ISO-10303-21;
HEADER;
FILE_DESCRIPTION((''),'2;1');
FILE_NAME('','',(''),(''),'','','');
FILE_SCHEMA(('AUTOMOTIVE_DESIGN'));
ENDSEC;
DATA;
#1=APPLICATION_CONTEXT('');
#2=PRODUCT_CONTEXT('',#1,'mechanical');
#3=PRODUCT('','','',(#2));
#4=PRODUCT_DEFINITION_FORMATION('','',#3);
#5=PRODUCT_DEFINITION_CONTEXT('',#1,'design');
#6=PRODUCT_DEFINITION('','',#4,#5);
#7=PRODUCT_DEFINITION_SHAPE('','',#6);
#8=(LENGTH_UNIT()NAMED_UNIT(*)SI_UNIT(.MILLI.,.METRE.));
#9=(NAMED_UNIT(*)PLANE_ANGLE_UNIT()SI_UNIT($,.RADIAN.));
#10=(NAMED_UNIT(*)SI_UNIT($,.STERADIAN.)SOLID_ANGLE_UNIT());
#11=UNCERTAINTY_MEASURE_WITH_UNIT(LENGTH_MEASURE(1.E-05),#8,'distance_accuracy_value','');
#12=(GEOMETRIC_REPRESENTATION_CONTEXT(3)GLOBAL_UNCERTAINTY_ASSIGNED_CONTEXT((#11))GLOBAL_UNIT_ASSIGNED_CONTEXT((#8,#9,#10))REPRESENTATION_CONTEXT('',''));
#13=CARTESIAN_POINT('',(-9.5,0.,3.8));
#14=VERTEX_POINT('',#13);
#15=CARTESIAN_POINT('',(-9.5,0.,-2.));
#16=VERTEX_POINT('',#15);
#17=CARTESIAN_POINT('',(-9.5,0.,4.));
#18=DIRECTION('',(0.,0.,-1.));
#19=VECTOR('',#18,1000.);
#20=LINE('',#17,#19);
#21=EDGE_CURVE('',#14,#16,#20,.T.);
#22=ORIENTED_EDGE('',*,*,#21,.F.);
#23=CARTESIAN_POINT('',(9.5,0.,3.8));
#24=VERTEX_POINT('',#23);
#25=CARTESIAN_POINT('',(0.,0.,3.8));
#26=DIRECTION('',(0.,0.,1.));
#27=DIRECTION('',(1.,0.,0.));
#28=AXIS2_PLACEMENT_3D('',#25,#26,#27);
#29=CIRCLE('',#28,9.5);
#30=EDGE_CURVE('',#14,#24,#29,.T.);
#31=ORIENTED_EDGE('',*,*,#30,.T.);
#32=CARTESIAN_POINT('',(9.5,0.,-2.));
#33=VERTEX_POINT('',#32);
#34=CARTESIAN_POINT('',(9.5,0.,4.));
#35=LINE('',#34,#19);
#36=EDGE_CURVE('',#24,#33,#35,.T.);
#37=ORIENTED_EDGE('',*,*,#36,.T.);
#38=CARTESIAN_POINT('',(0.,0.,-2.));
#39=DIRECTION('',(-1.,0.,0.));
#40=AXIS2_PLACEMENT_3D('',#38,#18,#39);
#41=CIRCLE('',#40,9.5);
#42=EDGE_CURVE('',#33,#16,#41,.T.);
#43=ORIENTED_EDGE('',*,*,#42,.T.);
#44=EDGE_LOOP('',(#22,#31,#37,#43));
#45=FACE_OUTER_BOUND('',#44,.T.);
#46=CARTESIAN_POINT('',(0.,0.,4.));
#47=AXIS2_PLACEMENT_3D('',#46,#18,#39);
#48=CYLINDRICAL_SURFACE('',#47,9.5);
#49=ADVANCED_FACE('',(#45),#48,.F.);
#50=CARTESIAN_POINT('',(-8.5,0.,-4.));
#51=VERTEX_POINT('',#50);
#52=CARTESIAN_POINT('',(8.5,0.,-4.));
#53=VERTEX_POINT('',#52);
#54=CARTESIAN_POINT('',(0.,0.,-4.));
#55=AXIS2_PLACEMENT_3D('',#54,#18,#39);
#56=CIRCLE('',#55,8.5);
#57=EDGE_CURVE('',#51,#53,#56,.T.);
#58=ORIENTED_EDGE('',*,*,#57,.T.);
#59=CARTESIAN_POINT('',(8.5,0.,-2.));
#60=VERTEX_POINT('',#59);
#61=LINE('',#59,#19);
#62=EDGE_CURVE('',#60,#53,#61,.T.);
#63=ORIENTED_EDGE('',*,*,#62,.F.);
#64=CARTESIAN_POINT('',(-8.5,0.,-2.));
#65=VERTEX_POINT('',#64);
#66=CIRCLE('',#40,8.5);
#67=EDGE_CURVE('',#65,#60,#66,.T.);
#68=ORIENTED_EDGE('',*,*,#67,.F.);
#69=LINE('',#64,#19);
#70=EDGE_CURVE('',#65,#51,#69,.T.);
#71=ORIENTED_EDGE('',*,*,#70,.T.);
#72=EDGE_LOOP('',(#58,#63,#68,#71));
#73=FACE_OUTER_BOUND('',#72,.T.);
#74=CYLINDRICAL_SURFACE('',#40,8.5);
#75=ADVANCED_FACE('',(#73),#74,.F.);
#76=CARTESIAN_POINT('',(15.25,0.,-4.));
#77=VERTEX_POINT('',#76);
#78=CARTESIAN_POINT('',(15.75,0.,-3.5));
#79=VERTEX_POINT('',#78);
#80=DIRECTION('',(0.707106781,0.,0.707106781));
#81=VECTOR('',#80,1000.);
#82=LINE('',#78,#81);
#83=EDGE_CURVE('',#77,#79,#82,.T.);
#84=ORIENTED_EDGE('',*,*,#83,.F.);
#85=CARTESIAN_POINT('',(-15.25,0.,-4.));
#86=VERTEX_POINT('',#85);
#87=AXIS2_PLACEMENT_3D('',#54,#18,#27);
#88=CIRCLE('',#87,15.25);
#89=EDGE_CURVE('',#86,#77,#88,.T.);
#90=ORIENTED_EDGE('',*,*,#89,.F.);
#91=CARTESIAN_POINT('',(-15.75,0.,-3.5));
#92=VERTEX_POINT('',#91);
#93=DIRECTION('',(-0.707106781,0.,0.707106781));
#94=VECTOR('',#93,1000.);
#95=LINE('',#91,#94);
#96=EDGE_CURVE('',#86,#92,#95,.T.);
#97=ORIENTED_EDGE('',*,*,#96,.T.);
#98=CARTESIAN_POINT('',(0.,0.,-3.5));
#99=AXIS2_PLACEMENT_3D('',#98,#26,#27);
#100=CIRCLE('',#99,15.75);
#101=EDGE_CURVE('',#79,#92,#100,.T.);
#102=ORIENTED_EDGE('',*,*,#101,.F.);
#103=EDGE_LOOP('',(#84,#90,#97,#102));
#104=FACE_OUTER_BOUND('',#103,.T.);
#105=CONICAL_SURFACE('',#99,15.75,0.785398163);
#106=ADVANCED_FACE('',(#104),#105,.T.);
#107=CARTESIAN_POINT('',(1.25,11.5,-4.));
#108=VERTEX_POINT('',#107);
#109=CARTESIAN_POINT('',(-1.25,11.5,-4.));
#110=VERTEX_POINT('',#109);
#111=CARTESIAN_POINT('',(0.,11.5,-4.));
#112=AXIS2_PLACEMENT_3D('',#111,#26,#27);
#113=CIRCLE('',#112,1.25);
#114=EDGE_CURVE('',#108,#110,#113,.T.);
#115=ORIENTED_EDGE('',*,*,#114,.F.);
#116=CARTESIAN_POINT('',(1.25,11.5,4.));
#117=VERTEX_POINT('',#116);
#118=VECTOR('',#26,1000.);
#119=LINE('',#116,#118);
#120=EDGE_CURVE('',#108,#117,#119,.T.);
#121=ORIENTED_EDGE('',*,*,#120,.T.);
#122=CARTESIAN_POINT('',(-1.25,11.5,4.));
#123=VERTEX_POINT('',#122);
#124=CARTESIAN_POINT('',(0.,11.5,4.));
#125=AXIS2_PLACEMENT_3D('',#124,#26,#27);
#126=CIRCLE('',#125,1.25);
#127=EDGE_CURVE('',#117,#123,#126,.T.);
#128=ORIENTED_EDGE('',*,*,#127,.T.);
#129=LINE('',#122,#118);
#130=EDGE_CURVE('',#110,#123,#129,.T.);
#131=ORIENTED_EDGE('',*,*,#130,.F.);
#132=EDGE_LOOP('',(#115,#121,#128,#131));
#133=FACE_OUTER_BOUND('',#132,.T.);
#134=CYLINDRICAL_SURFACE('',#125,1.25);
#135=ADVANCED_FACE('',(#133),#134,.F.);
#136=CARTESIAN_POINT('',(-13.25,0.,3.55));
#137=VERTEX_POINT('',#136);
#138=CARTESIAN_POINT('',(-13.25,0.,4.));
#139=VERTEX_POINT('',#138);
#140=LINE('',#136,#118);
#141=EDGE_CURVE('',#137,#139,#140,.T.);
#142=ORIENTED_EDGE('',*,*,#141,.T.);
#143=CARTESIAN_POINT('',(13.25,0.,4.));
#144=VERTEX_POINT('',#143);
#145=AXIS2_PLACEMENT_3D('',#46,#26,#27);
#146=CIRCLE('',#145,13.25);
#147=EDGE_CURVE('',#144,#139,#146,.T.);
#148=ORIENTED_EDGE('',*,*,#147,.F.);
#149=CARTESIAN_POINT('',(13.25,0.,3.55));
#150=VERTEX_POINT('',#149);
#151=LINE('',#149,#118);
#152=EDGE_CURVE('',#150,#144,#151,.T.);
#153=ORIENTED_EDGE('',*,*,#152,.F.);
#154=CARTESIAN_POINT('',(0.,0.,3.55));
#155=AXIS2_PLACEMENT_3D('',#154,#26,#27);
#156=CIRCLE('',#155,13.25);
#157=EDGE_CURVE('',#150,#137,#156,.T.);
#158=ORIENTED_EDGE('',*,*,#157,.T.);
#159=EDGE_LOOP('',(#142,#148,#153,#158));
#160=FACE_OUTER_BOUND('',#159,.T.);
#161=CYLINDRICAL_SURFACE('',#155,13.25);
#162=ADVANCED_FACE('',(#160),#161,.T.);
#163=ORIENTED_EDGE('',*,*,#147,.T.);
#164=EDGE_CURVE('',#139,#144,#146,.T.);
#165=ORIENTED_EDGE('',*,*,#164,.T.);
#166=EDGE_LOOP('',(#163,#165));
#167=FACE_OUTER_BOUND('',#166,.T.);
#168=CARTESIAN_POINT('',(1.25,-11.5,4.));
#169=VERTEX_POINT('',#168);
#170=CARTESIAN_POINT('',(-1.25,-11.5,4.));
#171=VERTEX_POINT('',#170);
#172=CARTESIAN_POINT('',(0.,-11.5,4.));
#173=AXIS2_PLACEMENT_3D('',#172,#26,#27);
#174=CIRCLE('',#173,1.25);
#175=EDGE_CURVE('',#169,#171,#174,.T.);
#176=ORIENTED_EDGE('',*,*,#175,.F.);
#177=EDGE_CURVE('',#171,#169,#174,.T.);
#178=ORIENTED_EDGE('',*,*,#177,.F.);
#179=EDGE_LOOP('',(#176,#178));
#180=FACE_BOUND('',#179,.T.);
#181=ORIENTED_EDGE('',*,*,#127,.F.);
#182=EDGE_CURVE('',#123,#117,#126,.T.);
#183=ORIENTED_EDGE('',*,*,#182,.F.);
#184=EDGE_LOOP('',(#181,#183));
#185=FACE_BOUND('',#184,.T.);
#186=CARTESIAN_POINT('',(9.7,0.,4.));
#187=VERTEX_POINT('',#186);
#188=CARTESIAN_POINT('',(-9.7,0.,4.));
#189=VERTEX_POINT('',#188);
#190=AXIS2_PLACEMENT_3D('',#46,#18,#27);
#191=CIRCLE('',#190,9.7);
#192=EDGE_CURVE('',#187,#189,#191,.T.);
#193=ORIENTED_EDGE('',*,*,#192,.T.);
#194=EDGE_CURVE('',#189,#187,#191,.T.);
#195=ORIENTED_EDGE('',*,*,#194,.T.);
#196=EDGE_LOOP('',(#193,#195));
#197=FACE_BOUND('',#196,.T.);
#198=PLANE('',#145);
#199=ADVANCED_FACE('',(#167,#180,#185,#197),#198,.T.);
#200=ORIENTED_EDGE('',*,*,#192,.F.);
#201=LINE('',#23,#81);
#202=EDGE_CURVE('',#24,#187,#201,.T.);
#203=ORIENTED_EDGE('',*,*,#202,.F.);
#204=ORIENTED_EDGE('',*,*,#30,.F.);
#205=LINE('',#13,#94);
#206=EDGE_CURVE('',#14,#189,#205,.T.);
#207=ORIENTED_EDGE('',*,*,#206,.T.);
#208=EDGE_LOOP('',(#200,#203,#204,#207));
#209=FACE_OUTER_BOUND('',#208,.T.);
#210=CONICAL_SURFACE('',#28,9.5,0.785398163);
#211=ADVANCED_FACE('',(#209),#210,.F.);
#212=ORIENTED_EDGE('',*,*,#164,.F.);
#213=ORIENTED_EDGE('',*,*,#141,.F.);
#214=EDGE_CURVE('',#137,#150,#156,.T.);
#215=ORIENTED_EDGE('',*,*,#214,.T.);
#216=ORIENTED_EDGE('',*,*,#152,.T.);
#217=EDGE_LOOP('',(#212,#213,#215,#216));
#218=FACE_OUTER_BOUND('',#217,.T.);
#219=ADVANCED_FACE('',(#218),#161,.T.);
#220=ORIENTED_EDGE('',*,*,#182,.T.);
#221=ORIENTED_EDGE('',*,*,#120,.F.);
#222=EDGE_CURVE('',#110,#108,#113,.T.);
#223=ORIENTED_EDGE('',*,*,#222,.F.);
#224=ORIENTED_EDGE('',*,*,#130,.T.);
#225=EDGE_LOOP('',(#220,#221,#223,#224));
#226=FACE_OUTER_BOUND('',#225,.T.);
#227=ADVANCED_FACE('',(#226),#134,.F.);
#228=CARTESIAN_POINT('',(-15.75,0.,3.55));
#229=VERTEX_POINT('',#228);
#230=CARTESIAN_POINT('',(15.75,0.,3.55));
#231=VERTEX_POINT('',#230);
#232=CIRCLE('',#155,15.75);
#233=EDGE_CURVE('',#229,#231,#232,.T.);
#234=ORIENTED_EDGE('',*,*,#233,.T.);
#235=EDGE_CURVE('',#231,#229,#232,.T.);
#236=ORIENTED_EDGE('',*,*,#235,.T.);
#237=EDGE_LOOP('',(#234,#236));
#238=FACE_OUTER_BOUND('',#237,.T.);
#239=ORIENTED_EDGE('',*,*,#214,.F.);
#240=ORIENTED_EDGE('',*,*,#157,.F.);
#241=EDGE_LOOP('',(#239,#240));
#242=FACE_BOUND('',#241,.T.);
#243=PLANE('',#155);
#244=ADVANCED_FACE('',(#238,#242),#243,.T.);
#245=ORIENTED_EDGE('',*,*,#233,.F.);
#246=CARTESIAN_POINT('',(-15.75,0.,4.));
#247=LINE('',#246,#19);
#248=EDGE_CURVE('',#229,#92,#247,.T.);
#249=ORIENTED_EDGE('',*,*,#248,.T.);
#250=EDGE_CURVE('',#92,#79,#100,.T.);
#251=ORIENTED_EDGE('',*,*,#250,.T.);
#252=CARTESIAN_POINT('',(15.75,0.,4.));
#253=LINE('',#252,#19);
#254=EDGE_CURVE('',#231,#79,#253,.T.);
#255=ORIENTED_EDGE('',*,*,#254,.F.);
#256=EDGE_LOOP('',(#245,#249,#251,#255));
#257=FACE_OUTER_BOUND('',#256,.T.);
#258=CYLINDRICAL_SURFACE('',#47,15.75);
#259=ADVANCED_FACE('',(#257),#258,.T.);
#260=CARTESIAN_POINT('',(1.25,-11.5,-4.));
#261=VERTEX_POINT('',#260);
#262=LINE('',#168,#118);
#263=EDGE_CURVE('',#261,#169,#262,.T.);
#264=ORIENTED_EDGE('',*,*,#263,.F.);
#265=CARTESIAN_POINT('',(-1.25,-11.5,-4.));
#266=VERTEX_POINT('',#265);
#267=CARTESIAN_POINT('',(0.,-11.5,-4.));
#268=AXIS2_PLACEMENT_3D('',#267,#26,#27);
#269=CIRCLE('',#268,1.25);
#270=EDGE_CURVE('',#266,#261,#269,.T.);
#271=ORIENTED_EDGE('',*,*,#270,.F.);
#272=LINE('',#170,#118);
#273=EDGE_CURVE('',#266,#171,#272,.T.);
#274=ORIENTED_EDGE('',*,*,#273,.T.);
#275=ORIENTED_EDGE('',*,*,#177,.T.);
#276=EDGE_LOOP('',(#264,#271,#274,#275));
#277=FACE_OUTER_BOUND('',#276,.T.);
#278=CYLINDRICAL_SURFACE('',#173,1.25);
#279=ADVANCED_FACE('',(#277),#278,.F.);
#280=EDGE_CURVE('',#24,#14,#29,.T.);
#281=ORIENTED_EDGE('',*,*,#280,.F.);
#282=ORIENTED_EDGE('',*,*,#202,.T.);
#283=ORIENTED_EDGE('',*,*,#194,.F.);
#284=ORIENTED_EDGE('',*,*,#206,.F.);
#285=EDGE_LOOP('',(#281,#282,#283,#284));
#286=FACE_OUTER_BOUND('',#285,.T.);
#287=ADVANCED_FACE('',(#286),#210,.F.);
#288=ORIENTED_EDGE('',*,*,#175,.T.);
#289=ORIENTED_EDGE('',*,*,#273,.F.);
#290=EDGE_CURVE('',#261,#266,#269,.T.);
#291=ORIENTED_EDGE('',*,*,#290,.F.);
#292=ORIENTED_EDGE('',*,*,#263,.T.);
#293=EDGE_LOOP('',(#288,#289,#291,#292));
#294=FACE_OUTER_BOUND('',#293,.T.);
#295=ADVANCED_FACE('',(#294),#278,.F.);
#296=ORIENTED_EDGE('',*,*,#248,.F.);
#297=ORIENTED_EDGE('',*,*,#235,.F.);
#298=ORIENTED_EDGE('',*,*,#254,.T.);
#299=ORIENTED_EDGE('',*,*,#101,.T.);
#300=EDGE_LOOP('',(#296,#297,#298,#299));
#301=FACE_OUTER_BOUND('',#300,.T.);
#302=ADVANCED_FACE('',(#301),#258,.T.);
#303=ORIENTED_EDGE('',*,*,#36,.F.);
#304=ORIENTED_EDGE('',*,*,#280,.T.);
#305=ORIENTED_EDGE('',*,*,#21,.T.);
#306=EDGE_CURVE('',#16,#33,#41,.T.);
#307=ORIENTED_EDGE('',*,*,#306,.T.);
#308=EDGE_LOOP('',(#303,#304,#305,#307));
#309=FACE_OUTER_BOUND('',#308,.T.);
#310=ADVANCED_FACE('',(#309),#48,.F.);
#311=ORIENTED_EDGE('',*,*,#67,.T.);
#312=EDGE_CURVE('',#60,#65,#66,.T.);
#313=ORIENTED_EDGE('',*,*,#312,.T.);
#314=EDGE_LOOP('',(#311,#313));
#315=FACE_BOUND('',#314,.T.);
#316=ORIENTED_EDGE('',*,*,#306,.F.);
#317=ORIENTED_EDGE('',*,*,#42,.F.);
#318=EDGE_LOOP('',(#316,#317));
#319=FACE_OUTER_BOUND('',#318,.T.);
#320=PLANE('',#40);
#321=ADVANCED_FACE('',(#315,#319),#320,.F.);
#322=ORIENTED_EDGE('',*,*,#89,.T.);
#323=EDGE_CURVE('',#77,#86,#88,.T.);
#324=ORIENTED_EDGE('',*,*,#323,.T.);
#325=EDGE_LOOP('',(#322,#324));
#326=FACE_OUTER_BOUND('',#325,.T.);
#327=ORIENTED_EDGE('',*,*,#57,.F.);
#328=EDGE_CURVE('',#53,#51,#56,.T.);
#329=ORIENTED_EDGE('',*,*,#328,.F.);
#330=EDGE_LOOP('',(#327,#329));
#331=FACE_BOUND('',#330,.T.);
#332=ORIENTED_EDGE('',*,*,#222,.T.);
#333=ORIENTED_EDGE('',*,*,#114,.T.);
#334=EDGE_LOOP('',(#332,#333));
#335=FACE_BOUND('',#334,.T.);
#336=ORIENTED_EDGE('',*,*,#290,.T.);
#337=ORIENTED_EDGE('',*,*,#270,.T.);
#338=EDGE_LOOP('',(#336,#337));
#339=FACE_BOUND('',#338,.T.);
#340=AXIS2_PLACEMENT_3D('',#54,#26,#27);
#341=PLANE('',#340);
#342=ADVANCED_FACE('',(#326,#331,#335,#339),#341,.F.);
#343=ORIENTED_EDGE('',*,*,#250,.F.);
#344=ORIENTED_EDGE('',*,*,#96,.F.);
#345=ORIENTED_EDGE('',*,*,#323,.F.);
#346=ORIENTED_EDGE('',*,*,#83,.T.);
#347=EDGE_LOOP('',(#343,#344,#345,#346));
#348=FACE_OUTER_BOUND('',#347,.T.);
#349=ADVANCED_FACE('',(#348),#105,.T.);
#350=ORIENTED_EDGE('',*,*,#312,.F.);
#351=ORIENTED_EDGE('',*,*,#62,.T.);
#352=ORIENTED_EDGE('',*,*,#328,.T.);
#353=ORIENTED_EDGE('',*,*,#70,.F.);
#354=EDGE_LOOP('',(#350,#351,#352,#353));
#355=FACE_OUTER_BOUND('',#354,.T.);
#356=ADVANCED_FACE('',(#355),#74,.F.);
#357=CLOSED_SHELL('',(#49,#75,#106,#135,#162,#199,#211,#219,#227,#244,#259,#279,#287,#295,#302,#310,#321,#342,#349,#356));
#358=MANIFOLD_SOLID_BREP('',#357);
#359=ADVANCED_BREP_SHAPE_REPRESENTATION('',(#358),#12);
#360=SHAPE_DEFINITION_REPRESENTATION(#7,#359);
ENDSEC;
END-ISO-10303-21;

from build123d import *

# Parameters (mm, degrees)
SKETCH1_R           = 15.75
SKETCH1_R_2         = 9.5
BOSS_EXTRUDE1_DEPTH = 4
SKETCH3_R           = 10.639095477
SKETCH3_R_2         = 8.5
BOSS_EXTRUDE2_DEPTH = 2
M3_TAPPED_HOLE1_D   = 2.5
CHAMFER1_SIZE       = 0.2
SKETCH6_R           = 20.677002962
SKETCH6_R_2         = 13.25
CUT_EXTRUDE1_DEPTH  = 0.45
CHAMFER2_SIZE       = 0.5


with BuildPart() as part:
    # Sketch1 → Boss-Extrude1 (new, symmetric)
    with BuildSketch(Plane.XY):
        Circle(SKETCH1_R)
        Circle(SKETCH1_R_2, mode=Mode.SUBTRACT)
    extrude(amount=BOSS_EXTRUDE1_DEPTH, both=True)

    # Sketch3 → Boss-Extrude2 (add)
    with BuildSketch(Plane(origin=(0, 0, -4), x_dir=(-1, 0, 0), z_dir=(0, 0, -1))):
        Circle(SKETCH3_R)
        Circle(SKETCH3_R_2, mode=Mode.SUBTRACT)
    extrude(amount=-BOSS_EXTRUDE2_DEPTH)

    # M3 Tapped Hole1 (through all)
    with Locations(Plane.XY.offset(4)):
        with Locations((0, -11.5)):
            m3_tapped_hole1 = Hole(M3_TAPPED_HOLE1_D / 2)

    # Mirror1: M3 Tapped Hole1 across plane
    add(m3_tapped_hole1.mirror(Plane.ZX), mode=Mode.SUBTRACT)

    # Chamfer1
    chamfer1_edges = [part.edges().sort_by_distance(p)[0] for p in [
        (-9.5, 0, 4),
    ]]
    chamfer(chamfer1_edges, length=CHAMFER1_SIZE)

    # Sketch6 → Cut-Extrude1 (cut)
    with BuildSketch(Plane.XY.offset(4)):
        Circle(SKETCH6_R)
        Circle(SKETCH6_R_2, mode=Mode.SUBTRACT)
    extrude(amount=-CUT_EXTRUDE1_DEPTH, mode=Mode.SUBTRACT)

    # Chamfer2
    chamfer2_edges = [part.edges().sort_by_distance(p)[0] for p in [
        (-15.75, 0, -4),
    ]]
    chamfer(chamfer2_edges, length=CHAMFER2_SIZE)


solid = part.part
